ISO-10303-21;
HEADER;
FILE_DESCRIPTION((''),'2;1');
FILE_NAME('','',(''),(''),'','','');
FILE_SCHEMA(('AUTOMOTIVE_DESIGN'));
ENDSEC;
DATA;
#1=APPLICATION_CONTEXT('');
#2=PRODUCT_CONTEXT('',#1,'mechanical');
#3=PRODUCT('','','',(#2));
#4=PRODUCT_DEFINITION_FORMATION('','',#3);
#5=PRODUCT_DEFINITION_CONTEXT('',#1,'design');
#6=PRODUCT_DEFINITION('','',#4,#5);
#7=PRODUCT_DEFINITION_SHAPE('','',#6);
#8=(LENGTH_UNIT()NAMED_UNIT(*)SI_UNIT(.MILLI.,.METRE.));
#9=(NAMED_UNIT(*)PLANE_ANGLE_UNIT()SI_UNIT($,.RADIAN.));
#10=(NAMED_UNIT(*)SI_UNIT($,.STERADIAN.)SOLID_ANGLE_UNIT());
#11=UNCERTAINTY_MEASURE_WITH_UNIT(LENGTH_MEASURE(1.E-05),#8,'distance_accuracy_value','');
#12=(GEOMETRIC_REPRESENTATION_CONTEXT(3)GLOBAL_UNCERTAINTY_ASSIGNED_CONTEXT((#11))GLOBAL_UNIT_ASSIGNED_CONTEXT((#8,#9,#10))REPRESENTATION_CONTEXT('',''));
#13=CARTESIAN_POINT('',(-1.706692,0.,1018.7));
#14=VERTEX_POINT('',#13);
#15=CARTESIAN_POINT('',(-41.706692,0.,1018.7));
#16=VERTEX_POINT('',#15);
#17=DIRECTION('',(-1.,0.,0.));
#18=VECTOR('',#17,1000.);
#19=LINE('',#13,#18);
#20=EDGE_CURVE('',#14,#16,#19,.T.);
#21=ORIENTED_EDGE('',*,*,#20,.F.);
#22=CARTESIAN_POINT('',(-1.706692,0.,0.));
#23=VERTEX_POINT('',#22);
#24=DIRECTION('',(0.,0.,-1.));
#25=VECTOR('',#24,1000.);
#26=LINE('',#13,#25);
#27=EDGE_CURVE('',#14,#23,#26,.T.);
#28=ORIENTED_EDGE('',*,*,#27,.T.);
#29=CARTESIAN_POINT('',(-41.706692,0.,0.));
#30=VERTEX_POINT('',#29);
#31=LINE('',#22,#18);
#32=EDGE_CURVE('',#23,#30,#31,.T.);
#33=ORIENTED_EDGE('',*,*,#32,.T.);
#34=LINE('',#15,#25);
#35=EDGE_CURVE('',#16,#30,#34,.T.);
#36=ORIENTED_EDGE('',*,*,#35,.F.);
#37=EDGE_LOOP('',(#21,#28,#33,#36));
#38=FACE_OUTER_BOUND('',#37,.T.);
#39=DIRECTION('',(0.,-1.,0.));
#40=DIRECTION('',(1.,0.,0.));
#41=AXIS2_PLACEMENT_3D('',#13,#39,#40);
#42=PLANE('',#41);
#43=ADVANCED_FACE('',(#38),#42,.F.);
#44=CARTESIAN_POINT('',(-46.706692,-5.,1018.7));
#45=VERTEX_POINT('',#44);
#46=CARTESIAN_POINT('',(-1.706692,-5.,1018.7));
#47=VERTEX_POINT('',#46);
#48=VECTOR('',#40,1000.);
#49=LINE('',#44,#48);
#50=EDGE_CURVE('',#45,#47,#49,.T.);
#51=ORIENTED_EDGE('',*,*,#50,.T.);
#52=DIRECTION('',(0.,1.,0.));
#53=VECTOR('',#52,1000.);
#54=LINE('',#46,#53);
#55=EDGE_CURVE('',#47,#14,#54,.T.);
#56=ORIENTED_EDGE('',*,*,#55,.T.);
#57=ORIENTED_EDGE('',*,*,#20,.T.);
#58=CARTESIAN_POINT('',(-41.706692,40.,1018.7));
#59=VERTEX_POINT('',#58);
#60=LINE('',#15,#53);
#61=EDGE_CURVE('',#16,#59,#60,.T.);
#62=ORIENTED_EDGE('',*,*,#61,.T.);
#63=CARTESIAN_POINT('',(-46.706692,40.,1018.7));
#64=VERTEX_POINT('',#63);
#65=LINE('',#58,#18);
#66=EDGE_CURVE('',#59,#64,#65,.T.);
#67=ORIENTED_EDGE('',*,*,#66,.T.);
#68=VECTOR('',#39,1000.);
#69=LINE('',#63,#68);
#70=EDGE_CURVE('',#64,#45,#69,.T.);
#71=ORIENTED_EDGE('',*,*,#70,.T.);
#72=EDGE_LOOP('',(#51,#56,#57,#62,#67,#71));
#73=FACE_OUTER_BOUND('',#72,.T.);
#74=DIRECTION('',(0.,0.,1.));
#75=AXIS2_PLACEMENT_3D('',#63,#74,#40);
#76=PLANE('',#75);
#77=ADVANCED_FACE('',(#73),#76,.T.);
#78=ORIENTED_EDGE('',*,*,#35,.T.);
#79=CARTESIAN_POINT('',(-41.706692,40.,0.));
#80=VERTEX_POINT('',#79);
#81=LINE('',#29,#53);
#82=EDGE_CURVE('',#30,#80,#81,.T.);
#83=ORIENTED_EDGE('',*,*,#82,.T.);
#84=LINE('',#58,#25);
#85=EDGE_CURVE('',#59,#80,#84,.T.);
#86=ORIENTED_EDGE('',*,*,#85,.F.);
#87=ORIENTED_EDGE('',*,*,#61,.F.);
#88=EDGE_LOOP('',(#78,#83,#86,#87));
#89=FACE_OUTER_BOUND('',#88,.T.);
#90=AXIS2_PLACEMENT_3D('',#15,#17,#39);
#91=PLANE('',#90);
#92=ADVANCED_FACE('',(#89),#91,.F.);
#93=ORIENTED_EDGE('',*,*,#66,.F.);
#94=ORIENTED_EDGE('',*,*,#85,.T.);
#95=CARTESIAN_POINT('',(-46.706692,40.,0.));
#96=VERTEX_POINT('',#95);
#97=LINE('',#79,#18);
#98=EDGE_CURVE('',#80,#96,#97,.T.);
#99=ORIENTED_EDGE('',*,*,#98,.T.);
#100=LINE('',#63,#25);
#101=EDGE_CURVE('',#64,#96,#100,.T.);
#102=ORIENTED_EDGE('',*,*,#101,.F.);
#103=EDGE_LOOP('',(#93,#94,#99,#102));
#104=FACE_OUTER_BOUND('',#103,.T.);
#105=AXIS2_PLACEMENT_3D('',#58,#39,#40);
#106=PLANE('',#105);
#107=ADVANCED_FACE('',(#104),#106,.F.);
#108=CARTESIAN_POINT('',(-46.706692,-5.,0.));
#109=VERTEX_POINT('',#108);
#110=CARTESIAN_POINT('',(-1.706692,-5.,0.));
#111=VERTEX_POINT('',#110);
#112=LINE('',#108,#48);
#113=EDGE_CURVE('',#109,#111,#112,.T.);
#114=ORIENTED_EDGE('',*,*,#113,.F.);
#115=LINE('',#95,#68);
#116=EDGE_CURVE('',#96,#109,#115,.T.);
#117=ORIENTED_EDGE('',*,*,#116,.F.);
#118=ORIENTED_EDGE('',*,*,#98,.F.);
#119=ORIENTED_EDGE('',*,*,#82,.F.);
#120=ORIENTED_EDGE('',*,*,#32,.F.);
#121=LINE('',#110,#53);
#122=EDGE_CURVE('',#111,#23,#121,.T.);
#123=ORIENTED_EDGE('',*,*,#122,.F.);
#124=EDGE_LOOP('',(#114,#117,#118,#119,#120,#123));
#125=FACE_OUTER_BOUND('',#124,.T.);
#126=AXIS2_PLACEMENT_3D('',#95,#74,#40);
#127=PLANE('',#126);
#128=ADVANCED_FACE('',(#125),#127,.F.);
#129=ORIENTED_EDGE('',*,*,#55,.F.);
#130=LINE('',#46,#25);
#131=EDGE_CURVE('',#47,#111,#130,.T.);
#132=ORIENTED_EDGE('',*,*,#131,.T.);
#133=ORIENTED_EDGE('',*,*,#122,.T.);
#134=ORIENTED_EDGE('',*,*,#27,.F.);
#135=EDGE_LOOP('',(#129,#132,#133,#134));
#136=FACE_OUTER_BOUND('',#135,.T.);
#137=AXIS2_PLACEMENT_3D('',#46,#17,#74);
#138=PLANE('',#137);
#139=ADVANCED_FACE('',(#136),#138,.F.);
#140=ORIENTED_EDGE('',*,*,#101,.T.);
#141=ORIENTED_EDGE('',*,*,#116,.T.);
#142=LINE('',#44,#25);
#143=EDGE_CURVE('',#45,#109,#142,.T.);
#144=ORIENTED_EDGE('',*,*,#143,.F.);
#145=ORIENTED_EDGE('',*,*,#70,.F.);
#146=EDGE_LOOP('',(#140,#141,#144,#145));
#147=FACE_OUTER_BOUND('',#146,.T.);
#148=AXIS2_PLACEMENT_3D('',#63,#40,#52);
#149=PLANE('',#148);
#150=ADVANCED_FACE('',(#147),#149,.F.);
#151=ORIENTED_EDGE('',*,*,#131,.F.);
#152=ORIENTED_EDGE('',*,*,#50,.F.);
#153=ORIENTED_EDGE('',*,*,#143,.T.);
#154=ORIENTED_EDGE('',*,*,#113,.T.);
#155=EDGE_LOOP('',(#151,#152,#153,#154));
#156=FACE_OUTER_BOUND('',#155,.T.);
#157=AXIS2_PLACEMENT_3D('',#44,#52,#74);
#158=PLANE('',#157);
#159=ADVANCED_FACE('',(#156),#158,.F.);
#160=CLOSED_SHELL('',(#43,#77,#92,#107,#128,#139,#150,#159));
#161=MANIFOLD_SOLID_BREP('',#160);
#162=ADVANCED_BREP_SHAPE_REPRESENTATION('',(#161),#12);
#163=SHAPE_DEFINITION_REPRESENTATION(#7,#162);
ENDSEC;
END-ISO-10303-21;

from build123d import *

# Parameters (mm, degrees)
EXTRUDE1_DEPTH = 1018.7


with BuildPart() as part:
    # Sketch1 → Extrude1 (new body)
    with BuildSketch(Plane.XY):
        Polygon((-46.706691722, 40), (-46.706691722, -5), (-1.706691722, -5), (-1.706691722, 0), (-41.706691722, 0), (-41.706691722, 40), align=None)
    extrude(amount=EXTRUDE1_DEPTH)


solid = part.part
